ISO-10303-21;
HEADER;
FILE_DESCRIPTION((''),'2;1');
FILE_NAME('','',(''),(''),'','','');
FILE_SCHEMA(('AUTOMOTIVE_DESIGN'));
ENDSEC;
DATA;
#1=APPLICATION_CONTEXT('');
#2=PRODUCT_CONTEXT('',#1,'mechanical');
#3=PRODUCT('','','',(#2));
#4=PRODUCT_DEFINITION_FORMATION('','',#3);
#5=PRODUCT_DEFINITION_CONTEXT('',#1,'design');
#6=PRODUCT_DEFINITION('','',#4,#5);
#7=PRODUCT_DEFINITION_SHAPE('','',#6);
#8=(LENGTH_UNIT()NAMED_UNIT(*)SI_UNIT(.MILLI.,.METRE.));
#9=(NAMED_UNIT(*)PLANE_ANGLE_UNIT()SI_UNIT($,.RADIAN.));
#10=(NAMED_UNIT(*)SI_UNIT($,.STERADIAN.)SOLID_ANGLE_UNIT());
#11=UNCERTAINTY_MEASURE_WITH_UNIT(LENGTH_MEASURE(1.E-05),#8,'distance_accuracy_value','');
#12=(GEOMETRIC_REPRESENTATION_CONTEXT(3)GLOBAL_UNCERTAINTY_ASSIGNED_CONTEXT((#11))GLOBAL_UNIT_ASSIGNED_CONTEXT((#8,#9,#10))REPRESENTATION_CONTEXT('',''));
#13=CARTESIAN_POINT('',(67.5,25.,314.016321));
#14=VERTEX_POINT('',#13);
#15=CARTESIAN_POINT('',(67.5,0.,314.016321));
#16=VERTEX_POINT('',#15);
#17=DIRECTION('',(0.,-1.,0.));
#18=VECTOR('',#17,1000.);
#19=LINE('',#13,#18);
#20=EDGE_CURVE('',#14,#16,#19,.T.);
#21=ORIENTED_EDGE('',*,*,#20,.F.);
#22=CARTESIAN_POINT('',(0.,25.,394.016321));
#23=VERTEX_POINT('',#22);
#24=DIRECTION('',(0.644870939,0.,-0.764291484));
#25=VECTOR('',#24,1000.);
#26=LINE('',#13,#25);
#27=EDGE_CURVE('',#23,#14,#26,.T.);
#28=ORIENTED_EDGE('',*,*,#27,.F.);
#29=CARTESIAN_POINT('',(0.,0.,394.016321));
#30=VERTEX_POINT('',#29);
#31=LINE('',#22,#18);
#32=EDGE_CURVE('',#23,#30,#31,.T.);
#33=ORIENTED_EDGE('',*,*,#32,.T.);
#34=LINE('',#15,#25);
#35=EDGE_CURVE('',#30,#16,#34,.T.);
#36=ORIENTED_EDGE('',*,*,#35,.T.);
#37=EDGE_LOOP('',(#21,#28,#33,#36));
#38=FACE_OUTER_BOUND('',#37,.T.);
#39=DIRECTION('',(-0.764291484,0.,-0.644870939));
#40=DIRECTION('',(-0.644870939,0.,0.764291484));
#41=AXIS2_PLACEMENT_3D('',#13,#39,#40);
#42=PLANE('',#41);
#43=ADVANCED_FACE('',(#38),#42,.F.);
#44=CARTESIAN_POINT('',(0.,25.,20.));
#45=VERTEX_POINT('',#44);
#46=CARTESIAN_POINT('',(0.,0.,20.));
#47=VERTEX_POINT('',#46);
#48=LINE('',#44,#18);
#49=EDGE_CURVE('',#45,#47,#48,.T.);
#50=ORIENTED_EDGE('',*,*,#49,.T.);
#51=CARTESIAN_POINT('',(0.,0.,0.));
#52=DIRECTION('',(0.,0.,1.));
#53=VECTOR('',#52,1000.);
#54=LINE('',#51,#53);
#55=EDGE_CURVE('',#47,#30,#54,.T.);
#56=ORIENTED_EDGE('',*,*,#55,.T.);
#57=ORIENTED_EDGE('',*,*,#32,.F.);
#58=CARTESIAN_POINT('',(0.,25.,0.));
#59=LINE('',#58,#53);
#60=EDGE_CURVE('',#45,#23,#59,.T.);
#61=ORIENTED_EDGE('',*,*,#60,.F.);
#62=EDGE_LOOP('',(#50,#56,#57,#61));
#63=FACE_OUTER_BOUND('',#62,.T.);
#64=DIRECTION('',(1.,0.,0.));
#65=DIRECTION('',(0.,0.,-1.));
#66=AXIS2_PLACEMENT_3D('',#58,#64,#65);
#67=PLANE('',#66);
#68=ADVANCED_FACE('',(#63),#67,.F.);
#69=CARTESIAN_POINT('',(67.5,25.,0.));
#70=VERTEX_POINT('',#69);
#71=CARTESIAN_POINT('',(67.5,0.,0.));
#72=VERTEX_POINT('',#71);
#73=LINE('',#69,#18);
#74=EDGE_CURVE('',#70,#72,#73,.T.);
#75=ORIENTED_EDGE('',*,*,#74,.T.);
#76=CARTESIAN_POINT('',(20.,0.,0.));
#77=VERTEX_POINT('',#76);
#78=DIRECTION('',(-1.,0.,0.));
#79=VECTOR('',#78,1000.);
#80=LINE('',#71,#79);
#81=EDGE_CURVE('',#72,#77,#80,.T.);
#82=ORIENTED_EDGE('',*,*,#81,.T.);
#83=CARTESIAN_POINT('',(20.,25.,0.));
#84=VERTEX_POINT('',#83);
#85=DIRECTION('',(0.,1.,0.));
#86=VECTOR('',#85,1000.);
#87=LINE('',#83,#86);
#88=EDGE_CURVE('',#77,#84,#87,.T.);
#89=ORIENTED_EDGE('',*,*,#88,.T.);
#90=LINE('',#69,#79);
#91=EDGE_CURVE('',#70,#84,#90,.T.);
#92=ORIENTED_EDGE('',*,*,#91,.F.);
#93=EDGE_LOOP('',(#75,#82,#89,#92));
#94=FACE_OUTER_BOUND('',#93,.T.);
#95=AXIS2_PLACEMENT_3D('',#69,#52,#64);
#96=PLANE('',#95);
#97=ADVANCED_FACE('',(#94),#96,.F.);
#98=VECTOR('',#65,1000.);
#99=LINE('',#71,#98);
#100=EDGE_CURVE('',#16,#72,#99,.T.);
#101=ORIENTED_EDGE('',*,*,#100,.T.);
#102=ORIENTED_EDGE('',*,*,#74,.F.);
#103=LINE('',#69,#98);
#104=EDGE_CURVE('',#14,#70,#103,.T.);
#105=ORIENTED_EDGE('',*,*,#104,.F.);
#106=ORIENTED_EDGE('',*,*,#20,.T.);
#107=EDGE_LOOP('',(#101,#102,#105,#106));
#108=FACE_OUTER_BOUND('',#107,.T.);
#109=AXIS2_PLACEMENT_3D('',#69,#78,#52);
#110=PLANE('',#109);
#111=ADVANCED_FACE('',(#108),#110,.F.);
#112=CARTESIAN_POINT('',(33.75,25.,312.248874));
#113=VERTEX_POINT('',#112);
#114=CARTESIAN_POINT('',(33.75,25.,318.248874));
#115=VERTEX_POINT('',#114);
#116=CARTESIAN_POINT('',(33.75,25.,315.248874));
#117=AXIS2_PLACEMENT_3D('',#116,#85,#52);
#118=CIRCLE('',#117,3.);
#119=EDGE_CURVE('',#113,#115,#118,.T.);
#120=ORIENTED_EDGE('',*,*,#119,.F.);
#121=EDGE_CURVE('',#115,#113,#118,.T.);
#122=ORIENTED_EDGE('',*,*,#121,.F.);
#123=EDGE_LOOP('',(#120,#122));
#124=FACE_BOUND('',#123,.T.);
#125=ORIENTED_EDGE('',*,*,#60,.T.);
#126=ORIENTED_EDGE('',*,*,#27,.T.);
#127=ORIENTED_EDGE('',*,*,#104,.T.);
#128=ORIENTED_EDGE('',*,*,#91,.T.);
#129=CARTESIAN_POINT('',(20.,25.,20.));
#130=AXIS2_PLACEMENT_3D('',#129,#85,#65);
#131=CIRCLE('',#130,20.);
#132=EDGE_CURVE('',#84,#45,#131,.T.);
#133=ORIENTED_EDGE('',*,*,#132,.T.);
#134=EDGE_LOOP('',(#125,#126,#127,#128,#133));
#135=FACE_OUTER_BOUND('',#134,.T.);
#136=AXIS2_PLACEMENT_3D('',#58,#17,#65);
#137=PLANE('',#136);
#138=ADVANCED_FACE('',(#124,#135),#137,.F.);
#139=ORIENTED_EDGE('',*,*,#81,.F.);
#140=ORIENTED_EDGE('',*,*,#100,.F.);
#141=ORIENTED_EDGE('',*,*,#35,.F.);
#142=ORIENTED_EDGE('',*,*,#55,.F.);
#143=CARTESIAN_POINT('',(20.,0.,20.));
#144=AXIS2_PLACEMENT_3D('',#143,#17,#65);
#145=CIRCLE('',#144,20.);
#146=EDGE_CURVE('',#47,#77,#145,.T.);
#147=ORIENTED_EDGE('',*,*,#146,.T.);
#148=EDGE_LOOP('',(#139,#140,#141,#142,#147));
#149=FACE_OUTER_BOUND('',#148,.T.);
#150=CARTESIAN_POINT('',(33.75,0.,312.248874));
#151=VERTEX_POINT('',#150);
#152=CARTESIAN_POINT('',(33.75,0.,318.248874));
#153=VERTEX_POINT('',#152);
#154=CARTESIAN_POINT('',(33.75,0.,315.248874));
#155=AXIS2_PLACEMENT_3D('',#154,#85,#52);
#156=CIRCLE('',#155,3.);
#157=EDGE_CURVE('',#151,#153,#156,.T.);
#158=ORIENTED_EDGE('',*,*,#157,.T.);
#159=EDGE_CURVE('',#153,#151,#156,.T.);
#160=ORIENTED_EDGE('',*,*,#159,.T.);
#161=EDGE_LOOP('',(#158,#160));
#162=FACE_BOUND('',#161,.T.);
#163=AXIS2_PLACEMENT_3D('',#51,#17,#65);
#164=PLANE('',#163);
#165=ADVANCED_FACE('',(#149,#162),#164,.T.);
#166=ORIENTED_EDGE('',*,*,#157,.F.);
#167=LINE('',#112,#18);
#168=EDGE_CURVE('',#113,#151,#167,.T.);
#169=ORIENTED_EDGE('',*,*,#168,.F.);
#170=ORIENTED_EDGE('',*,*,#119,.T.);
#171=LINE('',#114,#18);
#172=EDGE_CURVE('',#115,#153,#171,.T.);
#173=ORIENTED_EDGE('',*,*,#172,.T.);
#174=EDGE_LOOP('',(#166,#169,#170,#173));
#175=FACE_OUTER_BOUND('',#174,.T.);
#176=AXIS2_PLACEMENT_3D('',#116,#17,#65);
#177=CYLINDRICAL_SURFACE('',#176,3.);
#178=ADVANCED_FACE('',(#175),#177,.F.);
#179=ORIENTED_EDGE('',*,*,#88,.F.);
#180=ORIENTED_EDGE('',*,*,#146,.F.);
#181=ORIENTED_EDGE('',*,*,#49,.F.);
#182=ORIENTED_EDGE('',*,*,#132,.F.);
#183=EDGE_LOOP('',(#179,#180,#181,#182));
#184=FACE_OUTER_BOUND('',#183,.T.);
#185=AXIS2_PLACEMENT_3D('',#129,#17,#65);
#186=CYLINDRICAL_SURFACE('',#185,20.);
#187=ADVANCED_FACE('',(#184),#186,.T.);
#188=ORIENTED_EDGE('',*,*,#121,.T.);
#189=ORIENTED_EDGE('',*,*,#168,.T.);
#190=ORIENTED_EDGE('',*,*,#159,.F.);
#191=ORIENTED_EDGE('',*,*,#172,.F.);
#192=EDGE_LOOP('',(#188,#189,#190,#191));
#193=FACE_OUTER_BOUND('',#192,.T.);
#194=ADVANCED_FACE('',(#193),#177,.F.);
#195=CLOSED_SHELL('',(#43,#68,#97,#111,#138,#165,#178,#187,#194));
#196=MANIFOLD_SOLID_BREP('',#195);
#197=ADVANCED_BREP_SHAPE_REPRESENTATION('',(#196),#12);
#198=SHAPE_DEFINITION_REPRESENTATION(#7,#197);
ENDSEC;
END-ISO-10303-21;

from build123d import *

# Parameters (mm, degrees)
SKETCH1_R           = 3
BOSS_EXTRUDE1_DEPTH = 25
FILLET1_R           = 20


with BuildPart() as part:
    # Sketch1 → Boss-Extrude1 (new body)
    with BuildSketch(Plane(origin=(0, 0, 0), x_dir=(1, 0, 0), z_dir=(0, 1, 0))):
        Polygon((67.5, 0), (0, 0), (0, -394.016321232), (67.5, -314.016321232), align=None)
        with Locations(Location((33.75, -315.248874166, 0), (0, 0, 270))):
            Circle(SKETCH1_R, mode=Mode.SUBTRACT)
    extrude(amount=BOSS_EXTRUDE1_DEPTH)

    # Fillet1
    fillet1_edges = [part.edges().sort_by_distance(p)[0] for p in [
        (0, 12.5, 0),
    ]]
    fillet(fillet1_edges, radius=FILLET1_R)


solid = part.part
